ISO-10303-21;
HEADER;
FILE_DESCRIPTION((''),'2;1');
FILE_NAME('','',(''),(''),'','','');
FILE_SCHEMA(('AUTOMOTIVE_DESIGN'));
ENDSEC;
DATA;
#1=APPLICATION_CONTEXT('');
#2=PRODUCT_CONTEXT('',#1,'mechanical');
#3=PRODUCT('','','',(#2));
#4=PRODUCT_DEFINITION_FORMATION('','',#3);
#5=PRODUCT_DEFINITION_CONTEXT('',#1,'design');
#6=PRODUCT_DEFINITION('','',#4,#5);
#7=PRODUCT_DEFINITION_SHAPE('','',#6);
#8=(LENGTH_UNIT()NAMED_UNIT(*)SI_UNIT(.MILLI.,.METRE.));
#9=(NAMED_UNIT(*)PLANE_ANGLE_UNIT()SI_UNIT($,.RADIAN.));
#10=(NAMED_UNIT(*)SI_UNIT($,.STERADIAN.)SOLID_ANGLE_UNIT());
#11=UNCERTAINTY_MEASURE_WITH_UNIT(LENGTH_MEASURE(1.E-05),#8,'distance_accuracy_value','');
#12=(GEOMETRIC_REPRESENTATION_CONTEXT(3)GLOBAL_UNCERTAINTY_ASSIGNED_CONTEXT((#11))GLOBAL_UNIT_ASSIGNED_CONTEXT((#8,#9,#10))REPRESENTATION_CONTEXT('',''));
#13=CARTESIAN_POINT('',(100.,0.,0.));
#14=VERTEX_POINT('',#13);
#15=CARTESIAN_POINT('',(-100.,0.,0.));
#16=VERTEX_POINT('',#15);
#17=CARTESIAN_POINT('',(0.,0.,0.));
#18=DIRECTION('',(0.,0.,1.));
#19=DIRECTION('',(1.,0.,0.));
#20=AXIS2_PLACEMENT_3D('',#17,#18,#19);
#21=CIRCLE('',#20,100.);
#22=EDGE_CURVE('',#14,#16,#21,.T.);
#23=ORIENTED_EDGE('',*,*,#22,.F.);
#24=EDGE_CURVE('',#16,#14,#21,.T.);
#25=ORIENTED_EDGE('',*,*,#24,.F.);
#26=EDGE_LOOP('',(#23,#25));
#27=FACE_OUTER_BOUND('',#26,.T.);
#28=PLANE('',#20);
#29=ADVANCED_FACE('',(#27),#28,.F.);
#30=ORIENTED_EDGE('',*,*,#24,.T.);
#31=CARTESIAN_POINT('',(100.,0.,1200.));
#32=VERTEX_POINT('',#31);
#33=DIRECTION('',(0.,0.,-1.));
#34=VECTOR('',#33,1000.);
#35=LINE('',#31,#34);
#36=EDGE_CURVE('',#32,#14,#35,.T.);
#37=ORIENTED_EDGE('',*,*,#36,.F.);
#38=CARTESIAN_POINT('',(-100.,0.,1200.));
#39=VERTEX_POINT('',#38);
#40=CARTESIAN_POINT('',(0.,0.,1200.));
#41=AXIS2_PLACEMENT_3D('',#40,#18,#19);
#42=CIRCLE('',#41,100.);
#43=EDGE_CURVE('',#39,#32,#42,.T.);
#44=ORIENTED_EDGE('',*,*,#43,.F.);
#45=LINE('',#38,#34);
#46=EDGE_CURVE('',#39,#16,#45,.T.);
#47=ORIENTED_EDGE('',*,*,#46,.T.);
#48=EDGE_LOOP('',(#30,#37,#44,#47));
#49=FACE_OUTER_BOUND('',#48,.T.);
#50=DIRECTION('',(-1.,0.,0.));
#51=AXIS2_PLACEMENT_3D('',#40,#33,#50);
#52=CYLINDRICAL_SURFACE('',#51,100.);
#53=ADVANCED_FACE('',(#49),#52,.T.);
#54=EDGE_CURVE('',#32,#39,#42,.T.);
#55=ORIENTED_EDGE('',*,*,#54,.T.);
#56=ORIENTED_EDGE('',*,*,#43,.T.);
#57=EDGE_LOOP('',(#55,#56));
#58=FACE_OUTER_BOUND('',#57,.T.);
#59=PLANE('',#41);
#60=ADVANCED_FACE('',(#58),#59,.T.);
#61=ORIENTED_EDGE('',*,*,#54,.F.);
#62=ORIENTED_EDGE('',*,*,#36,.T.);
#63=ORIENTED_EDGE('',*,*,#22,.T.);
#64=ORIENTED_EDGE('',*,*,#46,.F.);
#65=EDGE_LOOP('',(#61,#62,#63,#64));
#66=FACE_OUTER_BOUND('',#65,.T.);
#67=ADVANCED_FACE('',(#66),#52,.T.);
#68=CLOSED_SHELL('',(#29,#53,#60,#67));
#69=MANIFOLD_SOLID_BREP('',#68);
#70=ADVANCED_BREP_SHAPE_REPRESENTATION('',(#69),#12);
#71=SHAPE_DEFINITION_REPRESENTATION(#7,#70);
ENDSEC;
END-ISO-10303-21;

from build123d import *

# Parameters (mm, degrees)
SKETCH1_R           = 100
BOSS_EXTRUDE1_DEPTH = 1200


with BuildPart() as part:
    # Sketch1 → Boss-Extrude1 (new body)
    with BuildSketch(Plane.XY):
        Circle(SKETCH1_R)
    extrude(amount=BOSS_EXTRUDE1_DEPTH)


solid = part.part
